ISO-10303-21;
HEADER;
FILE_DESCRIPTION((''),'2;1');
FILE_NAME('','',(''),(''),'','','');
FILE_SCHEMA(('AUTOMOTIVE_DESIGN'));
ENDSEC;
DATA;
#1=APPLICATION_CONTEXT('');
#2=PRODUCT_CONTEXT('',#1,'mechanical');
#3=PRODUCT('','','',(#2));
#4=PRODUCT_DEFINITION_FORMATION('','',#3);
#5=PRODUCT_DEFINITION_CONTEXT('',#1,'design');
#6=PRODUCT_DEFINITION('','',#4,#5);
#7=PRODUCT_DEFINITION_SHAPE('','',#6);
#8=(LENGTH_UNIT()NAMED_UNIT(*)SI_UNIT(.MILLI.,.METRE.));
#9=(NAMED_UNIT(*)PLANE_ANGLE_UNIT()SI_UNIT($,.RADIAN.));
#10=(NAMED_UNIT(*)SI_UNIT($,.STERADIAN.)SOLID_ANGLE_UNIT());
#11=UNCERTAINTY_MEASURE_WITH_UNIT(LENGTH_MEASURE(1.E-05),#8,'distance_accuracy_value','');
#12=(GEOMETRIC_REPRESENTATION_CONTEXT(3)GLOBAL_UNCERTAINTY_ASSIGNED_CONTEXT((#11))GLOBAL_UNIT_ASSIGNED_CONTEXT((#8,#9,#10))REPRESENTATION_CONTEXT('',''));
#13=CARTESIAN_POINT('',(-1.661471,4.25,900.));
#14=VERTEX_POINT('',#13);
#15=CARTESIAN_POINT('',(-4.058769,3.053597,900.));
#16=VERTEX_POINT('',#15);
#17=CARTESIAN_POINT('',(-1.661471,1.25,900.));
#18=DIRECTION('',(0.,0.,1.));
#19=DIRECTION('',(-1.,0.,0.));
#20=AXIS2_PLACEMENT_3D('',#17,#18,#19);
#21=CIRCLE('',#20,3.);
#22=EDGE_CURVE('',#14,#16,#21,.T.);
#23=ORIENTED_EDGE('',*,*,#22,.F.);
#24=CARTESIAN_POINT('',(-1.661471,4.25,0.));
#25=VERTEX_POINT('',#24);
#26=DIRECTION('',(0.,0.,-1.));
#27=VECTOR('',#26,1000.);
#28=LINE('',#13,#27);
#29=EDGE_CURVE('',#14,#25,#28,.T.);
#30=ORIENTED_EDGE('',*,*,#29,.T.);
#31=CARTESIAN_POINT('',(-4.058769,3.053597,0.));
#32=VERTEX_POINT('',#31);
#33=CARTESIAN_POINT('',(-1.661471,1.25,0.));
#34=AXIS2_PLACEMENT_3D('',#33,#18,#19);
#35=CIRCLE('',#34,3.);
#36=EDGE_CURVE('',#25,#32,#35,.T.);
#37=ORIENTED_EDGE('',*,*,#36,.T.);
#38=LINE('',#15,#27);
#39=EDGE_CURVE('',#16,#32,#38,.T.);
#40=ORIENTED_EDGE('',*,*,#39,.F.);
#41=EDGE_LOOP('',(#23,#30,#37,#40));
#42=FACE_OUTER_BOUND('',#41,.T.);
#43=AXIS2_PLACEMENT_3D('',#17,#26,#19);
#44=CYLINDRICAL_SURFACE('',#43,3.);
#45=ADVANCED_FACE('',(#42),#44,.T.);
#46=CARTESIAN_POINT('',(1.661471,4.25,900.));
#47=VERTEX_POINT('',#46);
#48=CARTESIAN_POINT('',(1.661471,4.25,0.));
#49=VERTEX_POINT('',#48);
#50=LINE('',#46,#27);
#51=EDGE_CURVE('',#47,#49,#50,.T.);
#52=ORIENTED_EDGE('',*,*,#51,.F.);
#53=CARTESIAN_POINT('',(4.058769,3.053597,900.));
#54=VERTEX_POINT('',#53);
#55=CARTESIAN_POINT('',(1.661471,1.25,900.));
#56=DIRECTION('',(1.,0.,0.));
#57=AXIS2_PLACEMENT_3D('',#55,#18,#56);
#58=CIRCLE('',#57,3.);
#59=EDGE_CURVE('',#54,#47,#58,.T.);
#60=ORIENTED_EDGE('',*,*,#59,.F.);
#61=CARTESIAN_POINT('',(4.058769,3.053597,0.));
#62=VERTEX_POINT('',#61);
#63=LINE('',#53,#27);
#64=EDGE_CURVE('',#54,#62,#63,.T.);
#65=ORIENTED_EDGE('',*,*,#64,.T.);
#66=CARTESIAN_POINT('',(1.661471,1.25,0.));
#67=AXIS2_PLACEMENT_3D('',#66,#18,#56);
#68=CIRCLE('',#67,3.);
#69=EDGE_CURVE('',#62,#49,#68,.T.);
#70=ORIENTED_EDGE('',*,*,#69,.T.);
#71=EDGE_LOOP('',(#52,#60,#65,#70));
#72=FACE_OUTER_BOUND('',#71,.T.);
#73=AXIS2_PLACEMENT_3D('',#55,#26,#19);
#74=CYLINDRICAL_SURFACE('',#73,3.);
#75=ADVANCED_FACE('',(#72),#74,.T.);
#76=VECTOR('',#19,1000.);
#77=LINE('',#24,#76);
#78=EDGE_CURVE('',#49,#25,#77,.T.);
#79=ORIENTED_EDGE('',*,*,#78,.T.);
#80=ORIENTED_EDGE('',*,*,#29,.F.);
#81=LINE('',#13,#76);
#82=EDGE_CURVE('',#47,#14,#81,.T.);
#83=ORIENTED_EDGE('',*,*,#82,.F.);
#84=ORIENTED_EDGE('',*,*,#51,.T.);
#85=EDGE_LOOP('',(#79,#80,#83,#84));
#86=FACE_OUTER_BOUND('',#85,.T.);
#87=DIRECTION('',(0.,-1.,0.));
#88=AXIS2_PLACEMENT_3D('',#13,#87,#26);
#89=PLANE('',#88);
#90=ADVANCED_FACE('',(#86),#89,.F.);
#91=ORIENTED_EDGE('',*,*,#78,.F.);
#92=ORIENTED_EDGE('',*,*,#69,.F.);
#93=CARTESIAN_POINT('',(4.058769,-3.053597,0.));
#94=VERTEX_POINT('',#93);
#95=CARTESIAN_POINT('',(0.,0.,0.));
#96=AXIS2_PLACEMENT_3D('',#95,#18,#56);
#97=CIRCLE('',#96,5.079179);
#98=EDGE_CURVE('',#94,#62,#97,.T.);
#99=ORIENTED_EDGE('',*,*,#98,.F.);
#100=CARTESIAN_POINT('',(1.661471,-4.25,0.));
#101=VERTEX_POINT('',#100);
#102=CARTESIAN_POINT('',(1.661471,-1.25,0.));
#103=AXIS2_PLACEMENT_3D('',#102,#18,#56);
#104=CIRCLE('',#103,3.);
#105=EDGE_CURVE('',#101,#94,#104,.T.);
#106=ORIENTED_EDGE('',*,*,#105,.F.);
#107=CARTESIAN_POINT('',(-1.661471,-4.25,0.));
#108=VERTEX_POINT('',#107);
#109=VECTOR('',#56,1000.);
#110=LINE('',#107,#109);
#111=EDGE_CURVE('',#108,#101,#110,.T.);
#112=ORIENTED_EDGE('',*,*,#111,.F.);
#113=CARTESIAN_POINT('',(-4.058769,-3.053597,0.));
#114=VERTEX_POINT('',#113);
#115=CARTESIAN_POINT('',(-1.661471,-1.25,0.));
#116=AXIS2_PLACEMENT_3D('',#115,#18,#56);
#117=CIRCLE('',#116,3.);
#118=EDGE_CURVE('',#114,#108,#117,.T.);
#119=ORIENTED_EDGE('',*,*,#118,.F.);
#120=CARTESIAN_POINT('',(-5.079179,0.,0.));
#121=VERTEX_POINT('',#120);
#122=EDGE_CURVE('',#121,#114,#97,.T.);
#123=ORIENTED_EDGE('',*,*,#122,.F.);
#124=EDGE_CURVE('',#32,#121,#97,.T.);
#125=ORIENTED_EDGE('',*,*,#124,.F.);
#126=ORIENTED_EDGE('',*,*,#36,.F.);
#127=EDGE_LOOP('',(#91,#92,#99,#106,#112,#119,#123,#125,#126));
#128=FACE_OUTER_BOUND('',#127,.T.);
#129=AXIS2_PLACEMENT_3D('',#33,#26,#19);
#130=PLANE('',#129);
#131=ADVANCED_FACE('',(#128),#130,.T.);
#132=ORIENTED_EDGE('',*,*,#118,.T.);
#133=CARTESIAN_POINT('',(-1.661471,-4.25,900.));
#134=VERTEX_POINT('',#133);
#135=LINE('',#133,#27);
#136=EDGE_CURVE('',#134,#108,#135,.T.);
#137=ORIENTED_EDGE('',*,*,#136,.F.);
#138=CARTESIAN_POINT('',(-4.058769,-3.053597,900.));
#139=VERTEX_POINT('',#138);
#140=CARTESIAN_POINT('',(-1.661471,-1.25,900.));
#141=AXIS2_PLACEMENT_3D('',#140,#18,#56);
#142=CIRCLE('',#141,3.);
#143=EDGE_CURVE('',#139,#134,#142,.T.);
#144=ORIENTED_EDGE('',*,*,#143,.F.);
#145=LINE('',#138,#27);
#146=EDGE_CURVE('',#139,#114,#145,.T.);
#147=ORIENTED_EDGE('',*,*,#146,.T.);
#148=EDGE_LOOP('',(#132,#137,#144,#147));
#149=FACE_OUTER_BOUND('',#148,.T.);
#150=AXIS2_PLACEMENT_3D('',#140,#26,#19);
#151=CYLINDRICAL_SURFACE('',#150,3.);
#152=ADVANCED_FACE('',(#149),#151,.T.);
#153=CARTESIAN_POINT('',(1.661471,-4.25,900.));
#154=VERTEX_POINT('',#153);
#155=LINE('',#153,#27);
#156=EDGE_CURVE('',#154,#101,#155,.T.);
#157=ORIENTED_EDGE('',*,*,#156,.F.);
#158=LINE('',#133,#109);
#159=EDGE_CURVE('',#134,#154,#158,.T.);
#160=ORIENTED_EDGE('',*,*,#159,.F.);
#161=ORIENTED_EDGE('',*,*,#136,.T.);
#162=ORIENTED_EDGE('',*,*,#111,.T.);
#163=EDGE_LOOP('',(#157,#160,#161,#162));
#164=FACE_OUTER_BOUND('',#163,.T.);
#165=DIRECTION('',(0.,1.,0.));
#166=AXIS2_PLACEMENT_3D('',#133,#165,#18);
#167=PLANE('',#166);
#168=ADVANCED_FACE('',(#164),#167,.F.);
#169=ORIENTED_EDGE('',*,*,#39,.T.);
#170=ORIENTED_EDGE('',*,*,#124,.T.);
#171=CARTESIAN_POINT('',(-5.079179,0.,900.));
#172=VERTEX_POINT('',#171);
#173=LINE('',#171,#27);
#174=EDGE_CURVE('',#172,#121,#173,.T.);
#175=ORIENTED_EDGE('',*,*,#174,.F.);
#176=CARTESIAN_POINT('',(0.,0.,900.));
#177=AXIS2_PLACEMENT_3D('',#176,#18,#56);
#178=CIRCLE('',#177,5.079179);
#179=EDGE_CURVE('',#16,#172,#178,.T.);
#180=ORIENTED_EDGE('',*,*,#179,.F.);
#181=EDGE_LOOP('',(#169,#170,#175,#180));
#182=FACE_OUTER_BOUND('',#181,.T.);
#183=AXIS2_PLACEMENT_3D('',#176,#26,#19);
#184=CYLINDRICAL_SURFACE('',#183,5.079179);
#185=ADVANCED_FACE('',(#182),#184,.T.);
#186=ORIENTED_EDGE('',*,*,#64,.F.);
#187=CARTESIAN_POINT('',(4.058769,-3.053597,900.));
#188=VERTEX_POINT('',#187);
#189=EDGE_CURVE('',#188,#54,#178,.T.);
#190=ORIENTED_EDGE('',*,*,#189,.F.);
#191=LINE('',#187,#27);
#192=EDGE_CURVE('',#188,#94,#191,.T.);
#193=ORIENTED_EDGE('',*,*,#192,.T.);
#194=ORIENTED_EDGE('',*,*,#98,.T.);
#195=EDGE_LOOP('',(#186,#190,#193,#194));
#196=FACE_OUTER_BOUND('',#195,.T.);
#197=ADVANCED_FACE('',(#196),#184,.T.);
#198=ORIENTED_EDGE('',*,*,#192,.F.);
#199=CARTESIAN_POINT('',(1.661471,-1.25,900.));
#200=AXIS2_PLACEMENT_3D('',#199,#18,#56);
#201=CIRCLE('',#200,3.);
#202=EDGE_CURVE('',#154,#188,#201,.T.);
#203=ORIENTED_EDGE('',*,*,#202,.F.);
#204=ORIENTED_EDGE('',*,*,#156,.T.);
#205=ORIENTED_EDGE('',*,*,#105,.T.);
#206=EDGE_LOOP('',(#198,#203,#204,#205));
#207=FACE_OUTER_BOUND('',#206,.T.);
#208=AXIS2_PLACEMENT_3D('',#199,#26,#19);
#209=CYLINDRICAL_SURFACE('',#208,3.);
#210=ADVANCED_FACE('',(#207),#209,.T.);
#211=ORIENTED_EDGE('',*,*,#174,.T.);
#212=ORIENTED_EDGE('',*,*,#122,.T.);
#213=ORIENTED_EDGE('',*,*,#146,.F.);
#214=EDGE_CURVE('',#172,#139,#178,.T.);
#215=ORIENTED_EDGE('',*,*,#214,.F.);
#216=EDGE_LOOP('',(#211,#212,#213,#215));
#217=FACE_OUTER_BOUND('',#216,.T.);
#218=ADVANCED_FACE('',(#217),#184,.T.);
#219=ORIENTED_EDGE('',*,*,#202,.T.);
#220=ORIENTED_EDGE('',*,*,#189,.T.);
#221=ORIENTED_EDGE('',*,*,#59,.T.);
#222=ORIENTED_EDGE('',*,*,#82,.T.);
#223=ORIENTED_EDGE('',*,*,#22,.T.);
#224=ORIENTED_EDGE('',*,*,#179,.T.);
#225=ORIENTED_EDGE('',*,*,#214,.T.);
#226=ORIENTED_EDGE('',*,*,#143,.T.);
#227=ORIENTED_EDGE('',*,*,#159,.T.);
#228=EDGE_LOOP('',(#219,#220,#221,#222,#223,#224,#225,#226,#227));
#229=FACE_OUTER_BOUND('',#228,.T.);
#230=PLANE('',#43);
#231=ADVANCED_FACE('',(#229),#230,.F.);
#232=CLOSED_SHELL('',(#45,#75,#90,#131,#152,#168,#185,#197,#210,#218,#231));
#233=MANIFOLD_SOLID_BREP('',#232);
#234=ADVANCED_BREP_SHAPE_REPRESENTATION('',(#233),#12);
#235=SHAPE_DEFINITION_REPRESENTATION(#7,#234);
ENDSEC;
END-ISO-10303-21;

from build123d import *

# Parameters (mm, degrees)
EXTRUDE_1_DEPTH = 900


with BuildPart() as part:
    # 草图1 → 拉伸1 (new body)
    with BuildSketch(Plane.XY):
        with BuildLine():
            Line((-1.661470687, 4.25), (1.661470687, 4.25))
            ThreePointArc((1.661470687, 4.25), (3.001099397, 3.934286669), (4.058769011, 3.053596614))
            ThreePointArc((4.058769011, 3.053596614), (5.079178887, 0), (4.058769011, -3.053596614))
            ThreePointArc((4.058769011, -3.053596614), (3.001099397, -3.934286669), (1.661470687, -4.25))
            Line((1.661470687, -4.25), (-1.661470687, -4.25))
            ThreePointArc((-1.661470687, -4.25), (-3.001099397, -3.934286669), (-4.058769011, -3.053596614))
            ThreePointArc((-4.058769011, -3.053596614), (-5.079178887, 0), (-4.058769011, 3.053596614))
            ThreePointArc((-4.058769011, 3.053596614), (-3.001099397, 3.934286669), (-1.661470687, 4.25))
        make_face()
    extrude(amount=EXTRUDE_1_DEPTH)


solid = part.part
